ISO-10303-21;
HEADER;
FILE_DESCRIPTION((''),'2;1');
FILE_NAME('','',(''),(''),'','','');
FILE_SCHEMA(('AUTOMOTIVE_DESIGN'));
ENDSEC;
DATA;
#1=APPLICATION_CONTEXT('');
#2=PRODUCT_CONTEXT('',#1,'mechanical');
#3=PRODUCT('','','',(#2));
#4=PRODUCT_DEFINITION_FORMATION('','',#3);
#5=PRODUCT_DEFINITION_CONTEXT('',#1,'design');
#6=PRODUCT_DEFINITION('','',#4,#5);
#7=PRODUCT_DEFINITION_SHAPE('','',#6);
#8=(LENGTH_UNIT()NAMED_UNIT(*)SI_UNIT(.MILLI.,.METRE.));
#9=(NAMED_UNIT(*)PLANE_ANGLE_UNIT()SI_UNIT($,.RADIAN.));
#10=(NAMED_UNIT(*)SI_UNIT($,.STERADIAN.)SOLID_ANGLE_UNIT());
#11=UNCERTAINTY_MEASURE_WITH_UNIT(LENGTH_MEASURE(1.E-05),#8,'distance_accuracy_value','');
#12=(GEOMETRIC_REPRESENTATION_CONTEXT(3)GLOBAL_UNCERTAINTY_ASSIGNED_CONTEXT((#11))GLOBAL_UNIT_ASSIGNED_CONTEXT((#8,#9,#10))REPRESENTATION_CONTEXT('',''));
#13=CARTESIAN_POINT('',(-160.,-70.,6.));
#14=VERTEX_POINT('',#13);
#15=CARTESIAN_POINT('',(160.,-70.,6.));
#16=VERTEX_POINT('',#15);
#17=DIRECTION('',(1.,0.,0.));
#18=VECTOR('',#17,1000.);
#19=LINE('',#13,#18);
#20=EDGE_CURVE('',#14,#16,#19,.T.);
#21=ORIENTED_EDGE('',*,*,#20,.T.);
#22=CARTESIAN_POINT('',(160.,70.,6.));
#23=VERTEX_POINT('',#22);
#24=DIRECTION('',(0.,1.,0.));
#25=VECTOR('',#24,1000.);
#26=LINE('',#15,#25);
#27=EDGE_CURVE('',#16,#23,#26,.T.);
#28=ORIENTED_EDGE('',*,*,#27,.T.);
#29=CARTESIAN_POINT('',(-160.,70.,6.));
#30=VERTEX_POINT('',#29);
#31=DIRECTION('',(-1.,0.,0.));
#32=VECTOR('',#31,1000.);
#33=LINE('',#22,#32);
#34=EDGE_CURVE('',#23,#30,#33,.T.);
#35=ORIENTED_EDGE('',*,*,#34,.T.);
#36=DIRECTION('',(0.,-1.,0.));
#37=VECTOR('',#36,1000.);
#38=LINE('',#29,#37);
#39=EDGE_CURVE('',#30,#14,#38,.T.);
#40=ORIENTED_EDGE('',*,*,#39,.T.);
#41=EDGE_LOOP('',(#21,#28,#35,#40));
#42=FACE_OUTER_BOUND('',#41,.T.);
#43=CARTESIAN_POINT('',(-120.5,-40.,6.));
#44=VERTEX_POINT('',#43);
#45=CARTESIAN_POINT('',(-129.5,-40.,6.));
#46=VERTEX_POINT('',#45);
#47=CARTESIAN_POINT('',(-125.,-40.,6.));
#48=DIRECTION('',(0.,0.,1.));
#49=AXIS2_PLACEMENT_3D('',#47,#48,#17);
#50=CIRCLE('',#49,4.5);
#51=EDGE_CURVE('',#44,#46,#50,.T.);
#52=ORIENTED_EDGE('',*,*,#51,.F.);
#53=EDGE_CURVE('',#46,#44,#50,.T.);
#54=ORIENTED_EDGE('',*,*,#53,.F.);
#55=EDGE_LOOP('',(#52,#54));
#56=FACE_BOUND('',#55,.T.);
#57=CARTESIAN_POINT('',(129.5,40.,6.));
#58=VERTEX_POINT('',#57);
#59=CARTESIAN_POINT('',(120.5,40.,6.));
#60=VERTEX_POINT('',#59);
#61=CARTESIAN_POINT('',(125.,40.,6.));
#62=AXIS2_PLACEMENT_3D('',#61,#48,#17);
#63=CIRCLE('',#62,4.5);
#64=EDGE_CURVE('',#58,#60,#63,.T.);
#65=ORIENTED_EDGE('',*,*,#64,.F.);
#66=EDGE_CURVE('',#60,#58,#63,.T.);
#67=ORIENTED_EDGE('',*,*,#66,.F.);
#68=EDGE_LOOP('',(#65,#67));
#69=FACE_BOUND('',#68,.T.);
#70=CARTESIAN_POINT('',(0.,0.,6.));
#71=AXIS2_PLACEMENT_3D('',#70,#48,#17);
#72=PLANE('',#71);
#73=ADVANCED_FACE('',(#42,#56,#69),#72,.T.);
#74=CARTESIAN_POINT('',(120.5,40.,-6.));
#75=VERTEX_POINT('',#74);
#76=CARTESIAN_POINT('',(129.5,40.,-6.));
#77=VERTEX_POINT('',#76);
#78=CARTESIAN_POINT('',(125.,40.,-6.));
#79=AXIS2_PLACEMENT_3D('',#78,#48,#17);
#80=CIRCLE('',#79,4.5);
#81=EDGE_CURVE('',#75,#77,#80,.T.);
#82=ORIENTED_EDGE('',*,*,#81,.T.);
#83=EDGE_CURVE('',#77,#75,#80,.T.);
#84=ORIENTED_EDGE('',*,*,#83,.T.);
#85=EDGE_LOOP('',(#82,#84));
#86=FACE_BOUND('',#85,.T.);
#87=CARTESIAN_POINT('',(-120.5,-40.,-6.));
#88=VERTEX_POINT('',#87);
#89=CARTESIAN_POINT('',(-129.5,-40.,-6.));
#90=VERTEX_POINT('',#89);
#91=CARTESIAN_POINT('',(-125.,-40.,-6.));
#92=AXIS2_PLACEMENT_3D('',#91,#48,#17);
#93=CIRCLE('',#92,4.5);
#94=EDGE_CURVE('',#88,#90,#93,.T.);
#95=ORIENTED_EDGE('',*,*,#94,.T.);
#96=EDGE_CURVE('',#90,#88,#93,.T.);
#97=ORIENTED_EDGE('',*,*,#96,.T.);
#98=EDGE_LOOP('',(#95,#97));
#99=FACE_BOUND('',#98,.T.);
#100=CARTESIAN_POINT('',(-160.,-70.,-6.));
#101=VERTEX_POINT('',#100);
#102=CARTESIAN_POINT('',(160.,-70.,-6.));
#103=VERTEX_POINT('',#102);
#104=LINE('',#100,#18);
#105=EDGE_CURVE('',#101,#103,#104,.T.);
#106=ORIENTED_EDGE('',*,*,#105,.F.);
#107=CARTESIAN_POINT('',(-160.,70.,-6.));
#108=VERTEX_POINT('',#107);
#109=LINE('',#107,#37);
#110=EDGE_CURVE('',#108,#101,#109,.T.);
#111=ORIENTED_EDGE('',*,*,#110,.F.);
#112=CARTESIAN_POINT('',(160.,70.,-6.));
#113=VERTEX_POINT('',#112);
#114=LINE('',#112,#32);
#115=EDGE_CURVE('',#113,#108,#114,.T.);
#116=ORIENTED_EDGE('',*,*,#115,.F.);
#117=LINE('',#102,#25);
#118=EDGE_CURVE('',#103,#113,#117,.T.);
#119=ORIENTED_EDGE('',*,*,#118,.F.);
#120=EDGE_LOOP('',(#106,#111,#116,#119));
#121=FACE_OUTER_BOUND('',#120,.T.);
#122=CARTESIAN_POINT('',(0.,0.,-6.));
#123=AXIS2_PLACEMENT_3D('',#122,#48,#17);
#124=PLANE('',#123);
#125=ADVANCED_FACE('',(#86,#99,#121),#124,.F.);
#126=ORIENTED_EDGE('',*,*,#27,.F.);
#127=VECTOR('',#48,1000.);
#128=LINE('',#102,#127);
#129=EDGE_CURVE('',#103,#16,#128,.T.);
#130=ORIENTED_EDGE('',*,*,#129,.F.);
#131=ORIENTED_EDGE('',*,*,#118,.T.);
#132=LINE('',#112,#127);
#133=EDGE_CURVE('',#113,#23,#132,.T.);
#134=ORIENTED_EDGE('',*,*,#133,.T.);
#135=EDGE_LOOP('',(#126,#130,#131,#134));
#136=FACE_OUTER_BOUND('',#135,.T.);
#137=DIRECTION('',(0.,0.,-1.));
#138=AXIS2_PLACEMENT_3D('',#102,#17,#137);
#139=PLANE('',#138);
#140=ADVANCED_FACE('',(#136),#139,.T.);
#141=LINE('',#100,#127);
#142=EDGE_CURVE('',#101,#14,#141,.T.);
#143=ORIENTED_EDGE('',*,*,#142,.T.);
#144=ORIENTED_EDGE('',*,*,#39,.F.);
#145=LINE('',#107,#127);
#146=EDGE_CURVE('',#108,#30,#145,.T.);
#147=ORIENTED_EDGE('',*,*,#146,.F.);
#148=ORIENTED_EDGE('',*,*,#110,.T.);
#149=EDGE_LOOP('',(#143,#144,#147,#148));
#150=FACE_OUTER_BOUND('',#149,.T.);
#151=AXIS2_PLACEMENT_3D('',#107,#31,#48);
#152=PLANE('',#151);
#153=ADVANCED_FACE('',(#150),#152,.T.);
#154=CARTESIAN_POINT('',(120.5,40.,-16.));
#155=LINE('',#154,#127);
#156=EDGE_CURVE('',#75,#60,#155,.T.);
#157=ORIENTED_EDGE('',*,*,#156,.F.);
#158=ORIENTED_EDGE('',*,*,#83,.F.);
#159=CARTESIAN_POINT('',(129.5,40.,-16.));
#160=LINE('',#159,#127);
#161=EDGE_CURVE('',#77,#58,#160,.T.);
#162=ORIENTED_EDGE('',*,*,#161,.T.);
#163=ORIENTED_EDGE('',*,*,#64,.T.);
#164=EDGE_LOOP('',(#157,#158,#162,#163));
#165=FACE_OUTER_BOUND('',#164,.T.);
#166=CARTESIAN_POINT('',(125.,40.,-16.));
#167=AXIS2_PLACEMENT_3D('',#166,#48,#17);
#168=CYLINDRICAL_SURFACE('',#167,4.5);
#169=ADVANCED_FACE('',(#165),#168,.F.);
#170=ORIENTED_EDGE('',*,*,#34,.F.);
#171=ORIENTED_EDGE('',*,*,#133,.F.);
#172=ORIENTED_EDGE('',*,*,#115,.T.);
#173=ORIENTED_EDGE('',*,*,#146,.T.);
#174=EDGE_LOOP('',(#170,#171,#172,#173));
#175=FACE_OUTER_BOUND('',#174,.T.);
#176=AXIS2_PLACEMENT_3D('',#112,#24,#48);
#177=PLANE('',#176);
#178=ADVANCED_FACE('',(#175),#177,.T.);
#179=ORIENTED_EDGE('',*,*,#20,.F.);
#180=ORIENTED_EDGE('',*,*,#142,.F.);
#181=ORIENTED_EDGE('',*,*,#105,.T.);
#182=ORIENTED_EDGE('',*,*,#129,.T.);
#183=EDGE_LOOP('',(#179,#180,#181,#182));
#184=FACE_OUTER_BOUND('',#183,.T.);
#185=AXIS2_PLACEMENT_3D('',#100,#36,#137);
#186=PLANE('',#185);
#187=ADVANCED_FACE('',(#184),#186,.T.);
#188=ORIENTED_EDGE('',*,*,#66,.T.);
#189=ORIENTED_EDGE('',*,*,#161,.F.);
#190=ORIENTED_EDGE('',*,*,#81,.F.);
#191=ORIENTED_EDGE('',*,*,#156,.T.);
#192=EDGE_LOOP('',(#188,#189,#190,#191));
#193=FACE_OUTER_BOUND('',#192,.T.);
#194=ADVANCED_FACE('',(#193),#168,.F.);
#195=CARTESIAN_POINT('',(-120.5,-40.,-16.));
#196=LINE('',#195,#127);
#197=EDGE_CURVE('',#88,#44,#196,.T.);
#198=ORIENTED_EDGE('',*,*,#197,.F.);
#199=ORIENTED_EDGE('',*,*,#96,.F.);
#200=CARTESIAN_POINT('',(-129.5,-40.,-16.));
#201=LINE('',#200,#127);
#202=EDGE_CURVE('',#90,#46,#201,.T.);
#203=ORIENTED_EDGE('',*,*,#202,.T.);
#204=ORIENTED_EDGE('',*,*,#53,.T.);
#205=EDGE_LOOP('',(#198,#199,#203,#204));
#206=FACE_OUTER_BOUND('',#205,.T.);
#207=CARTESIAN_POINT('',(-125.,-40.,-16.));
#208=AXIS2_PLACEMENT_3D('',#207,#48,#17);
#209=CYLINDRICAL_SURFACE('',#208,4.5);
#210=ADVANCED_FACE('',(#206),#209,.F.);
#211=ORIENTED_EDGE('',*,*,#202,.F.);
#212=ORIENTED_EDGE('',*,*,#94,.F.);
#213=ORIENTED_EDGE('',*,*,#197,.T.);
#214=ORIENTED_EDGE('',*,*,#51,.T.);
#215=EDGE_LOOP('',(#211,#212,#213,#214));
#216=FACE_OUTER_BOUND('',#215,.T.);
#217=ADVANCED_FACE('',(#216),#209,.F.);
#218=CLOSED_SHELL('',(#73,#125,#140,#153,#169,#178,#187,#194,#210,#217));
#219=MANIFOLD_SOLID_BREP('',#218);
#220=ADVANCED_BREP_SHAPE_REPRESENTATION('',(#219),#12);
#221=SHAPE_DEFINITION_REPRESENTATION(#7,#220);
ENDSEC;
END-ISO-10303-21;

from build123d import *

# Parameters (mm, degrees)
SKETCH_1_W          = 320
SKETCH_1_H          = 140
EXTRUDE_1_DEPTH     = 6
SKETCH_2_R          = 4.5
CUT_EXTRUDE_1_DEPTH = 16


with BuildPart() as part:
    # 草图1 → 凸台-拉伸1 (new, symmetric)
    with BuildSketch(Plane.XY):
        Rectangle(SKETCH_1_W, SKETCH_1_H)
    extrude(amount=EXTRUDE_1_DEPTH, both=True)

    # 草图2 → 切除-拉伸1 (cut, symmetric)
    with BuildSketch(Plane.XY):
        with Locations((-125, -40)):
            Circle(SKETCH_2_R)
        with Locations((125, 40)):
            Circle(SKETCH_2_R)
    extrude(amount=CUT_EXTRUDE_1_DEPTH, both=True, mode=Mode.SUBTRACT)


solid = part.part
